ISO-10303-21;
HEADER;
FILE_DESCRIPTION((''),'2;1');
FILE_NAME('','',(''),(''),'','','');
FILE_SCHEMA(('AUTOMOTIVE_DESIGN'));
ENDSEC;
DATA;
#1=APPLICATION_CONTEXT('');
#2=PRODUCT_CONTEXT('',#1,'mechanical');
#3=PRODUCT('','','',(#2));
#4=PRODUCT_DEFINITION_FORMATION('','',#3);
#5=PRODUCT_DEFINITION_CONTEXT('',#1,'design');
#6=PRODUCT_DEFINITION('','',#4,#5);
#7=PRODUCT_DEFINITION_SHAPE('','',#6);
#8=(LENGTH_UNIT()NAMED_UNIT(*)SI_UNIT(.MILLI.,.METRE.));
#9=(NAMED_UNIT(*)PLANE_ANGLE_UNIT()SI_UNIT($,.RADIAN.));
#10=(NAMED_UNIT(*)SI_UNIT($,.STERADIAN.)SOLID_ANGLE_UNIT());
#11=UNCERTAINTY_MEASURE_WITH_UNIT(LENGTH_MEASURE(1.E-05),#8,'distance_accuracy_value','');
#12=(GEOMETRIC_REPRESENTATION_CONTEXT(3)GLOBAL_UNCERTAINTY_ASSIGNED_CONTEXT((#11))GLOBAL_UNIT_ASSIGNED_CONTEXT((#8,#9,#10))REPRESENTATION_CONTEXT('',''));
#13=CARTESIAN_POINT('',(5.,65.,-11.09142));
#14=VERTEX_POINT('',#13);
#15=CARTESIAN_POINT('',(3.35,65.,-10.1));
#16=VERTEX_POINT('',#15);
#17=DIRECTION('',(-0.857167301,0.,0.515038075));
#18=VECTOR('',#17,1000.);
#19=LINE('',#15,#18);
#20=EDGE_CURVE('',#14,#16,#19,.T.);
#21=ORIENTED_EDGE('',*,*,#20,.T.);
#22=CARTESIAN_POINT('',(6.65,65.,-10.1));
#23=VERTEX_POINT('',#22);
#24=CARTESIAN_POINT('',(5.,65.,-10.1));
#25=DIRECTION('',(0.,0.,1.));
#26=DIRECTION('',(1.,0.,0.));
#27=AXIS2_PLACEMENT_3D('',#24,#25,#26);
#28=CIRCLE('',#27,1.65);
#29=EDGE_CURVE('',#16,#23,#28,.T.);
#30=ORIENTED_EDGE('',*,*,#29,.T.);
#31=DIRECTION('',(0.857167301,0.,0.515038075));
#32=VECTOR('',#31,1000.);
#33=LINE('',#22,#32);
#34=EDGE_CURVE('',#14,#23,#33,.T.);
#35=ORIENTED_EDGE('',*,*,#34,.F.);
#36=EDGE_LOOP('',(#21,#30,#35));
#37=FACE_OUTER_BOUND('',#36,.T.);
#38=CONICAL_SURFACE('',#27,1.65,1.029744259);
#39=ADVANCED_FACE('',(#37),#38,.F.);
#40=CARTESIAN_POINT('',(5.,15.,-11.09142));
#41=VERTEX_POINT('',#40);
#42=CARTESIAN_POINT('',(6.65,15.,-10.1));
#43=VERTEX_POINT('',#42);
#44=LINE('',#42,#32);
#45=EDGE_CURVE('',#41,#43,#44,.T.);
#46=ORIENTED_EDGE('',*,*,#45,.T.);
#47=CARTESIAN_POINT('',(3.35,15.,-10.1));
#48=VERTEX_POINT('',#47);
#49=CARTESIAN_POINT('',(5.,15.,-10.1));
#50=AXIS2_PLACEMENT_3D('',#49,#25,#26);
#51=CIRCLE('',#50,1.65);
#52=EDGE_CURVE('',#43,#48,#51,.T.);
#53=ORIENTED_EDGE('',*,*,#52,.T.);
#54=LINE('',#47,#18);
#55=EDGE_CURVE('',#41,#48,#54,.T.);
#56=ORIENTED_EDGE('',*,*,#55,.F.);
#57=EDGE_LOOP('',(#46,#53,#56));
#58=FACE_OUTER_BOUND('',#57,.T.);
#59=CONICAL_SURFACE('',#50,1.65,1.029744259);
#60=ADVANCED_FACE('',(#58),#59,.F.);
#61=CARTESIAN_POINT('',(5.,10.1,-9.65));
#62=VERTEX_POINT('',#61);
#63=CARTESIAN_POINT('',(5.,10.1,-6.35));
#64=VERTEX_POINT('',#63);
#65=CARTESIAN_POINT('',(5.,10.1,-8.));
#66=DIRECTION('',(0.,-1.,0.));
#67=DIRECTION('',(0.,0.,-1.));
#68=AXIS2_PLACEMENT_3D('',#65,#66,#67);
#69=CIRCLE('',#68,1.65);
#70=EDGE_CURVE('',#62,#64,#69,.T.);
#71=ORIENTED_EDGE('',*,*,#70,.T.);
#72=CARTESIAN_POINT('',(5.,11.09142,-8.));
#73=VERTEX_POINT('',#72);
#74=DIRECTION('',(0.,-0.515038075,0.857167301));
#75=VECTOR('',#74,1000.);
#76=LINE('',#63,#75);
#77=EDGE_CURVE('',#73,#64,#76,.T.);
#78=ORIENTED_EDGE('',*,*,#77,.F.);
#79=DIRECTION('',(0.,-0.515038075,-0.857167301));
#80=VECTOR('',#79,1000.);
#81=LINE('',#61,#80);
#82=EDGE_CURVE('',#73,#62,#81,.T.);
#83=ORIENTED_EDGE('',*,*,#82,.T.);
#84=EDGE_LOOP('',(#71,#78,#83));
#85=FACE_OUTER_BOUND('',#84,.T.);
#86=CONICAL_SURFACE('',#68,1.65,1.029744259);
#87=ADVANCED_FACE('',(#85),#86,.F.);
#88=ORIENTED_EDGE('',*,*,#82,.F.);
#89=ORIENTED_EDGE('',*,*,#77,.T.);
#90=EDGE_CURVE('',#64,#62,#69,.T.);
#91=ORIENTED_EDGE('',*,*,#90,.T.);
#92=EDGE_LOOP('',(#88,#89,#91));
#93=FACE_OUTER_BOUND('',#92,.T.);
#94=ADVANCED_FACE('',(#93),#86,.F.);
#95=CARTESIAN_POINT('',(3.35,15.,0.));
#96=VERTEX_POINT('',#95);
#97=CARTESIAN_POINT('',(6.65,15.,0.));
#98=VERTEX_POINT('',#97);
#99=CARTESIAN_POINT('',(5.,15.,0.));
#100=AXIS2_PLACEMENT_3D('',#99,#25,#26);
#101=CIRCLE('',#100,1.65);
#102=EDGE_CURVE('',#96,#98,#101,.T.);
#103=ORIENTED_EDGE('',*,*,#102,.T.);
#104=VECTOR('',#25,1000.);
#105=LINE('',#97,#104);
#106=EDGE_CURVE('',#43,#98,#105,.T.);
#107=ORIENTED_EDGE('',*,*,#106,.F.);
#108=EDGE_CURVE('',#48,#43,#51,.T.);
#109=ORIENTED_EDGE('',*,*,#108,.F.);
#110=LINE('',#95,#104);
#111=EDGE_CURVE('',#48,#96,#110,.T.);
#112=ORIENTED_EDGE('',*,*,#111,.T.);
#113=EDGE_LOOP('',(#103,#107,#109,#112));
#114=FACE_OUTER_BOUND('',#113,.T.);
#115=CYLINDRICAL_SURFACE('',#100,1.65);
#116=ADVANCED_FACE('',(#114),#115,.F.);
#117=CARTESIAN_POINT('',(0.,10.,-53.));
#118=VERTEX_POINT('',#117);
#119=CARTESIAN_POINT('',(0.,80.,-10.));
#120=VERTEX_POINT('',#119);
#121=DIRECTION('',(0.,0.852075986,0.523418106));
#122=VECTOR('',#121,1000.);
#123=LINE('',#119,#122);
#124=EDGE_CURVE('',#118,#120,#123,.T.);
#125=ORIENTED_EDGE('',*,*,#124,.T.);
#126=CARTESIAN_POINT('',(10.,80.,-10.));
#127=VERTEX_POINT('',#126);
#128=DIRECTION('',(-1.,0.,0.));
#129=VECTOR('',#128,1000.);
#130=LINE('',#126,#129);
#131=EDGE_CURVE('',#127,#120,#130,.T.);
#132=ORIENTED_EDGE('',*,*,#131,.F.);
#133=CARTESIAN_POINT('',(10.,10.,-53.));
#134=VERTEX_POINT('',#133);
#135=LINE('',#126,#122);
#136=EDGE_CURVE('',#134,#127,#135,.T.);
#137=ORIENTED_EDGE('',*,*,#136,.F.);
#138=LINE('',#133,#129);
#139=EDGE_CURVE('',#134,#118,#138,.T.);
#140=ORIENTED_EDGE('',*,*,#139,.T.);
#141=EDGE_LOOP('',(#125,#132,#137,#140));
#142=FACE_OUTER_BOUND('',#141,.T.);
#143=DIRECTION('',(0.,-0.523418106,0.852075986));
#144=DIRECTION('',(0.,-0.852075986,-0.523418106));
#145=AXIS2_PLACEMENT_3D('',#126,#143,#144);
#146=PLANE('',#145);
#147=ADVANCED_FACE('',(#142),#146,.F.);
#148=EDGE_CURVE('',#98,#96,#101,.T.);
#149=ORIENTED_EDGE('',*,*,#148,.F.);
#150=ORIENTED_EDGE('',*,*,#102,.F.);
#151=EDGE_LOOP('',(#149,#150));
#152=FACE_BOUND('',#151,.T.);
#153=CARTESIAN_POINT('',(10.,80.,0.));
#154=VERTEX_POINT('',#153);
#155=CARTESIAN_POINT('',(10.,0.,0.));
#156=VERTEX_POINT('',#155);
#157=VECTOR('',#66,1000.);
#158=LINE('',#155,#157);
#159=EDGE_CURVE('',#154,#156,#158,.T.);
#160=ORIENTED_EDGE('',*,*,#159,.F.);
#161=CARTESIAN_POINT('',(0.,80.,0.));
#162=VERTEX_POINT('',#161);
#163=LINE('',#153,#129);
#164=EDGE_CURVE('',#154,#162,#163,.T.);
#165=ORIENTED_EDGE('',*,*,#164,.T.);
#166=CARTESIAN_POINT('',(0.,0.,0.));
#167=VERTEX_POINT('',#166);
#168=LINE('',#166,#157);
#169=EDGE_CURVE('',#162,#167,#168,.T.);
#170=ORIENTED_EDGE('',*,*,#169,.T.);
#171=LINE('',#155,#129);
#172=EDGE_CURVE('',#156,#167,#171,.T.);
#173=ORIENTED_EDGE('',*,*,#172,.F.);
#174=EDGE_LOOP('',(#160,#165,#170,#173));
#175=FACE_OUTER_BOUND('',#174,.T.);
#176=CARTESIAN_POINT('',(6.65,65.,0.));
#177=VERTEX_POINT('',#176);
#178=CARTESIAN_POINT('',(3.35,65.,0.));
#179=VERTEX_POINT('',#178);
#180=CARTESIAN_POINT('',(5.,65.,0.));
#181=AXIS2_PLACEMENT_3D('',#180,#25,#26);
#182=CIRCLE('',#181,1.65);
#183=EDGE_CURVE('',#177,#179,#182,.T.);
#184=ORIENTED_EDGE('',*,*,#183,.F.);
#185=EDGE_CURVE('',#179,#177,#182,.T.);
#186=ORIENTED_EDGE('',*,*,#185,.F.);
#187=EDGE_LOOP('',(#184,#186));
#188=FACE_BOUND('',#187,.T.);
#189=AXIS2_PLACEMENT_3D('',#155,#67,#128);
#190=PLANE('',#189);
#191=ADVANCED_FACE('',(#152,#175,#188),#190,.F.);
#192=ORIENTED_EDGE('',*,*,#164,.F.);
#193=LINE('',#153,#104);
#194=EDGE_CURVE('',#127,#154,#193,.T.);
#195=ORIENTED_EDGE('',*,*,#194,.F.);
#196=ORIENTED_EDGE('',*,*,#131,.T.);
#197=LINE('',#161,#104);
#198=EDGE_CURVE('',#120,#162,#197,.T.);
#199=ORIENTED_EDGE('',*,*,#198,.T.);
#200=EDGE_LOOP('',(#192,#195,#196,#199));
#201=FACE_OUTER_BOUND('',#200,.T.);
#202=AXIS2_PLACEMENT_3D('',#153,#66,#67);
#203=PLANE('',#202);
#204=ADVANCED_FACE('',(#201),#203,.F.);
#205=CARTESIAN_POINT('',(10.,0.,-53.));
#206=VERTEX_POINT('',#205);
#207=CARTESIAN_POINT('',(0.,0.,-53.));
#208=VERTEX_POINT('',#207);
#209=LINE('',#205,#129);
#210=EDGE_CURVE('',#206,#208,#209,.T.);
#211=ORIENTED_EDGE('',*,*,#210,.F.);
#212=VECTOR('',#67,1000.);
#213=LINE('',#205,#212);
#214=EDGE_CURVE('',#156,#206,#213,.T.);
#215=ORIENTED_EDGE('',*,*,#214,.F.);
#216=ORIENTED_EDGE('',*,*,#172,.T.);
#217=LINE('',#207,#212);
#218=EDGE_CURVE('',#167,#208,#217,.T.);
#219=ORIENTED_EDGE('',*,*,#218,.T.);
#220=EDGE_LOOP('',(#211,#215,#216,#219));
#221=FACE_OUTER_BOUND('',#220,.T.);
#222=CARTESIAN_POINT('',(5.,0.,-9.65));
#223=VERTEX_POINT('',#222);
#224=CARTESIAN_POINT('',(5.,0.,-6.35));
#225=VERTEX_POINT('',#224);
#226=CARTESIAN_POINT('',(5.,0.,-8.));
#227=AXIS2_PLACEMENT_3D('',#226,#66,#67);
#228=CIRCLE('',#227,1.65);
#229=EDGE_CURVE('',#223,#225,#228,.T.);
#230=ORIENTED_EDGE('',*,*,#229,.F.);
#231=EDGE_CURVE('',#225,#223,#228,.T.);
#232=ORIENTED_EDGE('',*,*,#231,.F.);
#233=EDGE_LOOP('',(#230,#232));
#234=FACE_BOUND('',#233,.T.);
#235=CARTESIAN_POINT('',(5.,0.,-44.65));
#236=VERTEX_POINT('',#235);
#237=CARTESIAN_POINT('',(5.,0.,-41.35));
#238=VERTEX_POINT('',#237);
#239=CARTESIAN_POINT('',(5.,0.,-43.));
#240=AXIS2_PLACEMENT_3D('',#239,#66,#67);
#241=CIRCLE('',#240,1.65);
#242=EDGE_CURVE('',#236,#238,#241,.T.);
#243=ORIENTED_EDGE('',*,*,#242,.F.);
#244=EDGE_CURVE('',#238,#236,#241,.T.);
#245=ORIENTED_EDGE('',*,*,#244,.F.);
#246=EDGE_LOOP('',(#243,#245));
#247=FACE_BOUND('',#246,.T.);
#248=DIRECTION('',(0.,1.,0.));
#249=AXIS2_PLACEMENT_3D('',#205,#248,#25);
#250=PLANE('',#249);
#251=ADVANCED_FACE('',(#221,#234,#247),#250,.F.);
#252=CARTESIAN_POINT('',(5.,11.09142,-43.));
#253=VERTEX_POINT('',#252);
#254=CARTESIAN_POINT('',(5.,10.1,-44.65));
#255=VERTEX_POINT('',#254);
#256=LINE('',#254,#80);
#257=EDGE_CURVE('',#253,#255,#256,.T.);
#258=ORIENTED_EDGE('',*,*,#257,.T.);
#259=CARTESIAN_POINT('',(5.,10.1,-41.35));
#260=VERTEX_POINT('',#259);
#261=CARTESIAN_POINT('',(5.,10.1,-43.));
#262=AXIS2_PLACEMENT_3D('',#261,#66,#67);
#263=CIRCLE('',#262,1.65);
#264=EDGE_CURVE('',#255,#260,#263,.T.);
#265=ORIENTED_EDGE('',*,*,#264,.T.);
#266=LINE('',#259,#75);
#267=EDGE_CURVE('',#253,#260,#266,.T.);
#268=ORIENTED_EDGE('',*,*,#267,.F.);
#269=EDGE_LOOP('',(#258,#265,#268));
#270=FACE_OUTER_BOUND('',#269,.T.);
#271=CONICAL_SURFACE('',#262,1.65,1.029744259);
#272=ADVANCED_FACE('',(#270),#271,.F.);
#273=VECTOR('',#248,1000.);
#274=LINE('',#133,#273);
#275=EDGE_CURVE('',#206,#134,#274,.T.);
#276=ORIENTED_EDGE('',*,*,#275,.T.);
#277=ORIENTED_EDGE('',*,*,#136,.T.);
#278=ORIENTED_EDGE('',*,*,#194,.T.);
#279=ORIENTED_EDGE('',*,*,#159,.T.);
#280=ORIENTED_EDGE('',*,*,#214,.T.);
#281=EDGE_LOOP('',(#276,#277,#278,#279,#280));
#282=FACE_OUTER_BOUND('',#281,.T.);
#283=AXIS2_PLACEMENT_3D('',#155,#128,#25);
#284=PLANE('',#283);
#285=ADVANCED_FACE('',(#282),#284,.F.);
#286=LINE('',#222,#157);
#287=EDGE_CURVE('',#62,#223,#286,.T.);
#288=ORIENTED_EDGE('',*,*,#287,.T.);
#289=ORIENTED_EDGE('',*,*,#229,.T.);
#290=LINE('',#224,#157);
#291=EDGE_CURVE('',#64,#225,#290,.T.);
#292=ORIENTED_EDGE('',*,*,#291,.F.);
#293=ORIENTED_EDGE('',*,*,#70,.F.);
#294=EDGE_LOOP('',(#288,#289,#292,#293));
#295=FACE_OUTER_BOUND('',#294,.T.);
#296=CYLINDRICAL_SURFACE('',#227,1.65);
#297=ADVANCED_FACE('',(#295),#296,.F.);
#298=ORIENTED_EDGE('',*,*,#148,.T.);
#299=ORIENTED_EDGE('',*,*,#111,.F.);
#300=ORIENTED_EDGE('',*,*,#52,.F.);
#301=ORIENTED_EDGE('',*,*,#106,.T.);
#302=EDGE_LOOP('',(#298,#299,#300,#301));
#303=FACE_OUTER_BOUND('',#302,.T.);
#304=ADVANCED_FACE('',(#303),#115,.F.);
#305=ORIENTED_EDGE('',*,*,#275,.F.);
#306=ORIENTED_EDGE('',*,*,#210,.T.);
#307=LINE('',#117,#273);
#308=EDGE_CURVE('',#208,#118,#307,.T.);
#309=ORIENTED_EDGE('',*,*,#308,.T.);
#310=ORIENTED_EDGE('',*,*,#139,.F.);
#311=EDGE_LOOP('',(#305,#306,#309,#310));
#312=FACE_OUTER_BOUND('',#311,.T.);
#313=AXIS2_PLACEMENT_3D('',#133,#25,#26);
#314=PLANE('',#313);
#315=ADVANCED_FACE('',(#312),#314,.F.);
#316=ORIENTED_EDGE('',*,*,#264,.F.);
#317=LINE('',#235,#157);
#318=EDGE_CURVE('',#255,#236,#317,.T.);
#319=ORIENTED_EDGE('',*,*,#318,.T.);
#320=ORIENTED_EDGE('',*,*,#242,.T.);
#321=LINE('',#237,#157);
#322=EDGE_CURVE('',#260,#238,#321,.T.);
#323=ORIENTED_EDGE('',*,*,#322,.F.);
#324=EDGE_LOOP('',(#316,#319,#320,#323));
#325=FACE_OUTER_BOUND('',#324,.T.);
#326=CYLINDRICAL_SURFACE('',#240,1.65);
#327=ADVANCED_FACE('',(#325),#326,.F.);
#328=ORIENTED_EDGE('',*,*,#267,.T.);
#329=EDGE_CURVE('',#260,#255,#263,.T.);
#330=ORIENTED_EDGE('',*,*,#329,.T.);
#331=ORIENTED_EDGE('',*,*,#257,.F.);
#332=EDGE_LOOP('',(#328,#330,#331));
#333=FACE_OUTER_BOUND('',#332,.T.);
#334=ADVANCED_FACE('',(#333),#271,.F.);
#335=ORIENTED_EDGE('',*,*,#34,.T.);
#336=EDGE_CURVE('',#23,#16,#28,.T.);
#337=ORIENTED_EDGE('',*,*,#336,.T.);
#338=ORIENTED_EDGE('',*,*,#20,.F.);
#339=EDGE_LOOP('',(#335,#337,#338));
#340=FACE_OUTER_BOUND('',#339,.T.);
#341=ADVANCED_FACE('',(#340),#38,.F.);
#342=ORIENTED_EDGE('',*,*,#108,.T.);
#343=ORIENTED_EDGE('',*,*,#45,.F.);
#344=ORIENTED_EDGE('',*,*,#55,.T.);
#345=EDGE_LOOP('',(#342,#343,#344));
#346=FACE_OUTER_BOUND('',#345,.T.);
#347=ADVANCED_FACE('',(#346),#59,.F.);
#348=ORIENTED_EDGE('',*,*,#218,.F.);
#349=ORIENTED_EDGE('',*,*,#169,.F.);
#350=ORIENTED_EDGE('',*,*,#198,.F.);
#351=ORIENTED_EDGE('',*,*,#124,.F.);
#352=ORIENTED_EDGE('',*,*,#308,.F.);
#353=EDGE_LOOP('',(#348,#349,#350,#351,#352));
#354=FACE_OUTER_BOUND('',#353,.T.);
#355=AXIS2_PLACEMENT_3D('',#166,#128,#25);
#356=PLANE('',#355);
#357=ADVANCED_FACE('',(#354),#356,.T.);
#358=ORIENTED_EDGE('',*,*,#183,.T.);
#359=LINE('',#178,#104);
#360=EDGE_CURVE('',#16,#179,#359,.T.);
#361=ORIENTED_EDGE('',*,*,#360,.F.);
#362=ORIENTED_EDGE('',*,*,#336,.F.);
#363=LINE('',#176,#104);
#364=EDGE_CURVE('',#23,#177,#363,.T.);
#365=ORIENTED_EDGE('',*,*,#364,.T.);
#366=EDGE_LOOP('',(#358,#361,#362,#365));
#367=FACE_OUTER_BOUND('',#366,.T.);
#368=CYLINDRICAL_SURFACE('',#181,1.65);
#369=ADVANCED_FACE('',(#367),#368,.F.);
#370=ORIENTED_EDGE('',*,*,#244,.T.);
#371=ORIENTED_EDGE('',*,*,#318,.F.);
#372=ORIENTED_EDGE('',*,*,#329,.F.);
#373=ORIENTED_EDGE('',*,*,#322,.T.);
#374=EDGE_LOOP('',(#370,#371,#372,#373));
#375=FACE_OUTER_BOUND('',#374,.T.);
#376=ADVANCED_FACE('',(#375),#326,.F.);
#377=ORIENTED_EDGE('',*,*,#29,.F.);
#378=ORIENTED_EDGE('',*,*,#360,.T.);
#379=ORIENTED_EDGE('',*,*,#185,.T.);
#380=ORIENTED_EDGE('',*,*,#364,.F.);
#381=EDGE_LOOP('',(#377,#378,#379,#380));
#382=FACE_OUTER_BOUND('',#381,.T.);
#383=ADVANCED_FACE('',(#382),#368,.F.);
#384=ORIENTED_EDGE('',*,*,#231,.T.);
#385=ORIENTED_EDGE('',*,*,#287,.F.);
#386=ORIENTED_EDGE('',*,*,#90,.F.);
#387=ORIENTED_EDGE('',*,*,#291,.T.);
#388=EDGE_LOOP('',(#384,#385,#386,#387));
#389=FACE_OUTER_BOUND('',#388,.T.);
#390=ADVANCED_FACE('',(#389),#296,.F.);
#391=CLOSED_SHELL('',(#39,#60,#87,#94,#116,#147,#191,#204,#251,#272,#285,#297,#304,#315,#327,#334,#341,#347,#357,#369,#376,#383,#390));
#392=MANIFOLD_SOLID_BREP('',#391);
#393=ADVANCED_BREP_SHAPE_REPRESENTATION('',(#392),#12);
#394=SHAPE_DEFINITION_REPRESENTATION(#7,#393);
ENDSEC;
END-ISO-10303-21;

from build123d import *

# Parameters (mm, degrees)
BOSS_EXTRUDE1_DEPTH   = 10
M4_TAPPED_HOLE1_D     = 3.3
M4_TAPPED_HOLE1_DEPTH = 10.1
M4_TAPPED_HOLE1_TIP   = 0.991420021
M4_TAPPED_HOLE2_D     = 3.3
M4_TAPPED_HOLE2_DEPTH = 10.1
M4_TAPPED_HOLE2_TIP   = 0.991420021


with BuildPart() as part:
    # Sketch1 → Boss-Extrude1 (new body)
    with BuildSketch(Plane(origin=(0, 0, 0), x_dir=(0, 0, -1), z_dir=(1, 0, 0))):
        Polygon((0, 0), (0, 80), (10, 80), (53, 10), (53, 0), align=None)
    extrude(amount=BOSS_EXTRUDE1_DEPTH)

    # M4 Tapped Hole1
    with Locations(Plane.XY):
        with Locations((5, 65), (5, 15)):
            Hole(M4_TAPPED_HOLE1_D / 2, depth=M4_TAPPED_HOLE1_DEPTH)
            with Locations((0, 0, -(M4_TAPPED_HOLE1_DEPTH + M4_TAPPED_HOLE1_TIP / 2))):  # 118° drill point
                Cone(0, M4_TAPPED_HOLE1_D / 2, M4_TAPPED_HOLE1_TIP, mode=Mode.SUBTRACT)

    # M4 Tapped Hole2
    with Locations(Plane(origin=(0, 0, 0), x_dir=(-1, 0, 0), z_dir=(0, -1, 0))):
        with Locations((-5, 43), (-5, 8)):
            Hole(M4_TAPPED_HOLE2_D / 2, depth=M4_TAPPED_HOLE2_DEPTH)
            with Locations((0, 0, -(M4_TAPPED_HOLE2_DEPTH + M4_TAPPED_HOLE2_TIP / 2))):  # 118° drill point
                Cone(0, M4_TAPPED_HOLE2_D / 2, M4_TAPPED_HOLE2_TIP, mode=Mode.SUBTRACT)


solid = part.part
